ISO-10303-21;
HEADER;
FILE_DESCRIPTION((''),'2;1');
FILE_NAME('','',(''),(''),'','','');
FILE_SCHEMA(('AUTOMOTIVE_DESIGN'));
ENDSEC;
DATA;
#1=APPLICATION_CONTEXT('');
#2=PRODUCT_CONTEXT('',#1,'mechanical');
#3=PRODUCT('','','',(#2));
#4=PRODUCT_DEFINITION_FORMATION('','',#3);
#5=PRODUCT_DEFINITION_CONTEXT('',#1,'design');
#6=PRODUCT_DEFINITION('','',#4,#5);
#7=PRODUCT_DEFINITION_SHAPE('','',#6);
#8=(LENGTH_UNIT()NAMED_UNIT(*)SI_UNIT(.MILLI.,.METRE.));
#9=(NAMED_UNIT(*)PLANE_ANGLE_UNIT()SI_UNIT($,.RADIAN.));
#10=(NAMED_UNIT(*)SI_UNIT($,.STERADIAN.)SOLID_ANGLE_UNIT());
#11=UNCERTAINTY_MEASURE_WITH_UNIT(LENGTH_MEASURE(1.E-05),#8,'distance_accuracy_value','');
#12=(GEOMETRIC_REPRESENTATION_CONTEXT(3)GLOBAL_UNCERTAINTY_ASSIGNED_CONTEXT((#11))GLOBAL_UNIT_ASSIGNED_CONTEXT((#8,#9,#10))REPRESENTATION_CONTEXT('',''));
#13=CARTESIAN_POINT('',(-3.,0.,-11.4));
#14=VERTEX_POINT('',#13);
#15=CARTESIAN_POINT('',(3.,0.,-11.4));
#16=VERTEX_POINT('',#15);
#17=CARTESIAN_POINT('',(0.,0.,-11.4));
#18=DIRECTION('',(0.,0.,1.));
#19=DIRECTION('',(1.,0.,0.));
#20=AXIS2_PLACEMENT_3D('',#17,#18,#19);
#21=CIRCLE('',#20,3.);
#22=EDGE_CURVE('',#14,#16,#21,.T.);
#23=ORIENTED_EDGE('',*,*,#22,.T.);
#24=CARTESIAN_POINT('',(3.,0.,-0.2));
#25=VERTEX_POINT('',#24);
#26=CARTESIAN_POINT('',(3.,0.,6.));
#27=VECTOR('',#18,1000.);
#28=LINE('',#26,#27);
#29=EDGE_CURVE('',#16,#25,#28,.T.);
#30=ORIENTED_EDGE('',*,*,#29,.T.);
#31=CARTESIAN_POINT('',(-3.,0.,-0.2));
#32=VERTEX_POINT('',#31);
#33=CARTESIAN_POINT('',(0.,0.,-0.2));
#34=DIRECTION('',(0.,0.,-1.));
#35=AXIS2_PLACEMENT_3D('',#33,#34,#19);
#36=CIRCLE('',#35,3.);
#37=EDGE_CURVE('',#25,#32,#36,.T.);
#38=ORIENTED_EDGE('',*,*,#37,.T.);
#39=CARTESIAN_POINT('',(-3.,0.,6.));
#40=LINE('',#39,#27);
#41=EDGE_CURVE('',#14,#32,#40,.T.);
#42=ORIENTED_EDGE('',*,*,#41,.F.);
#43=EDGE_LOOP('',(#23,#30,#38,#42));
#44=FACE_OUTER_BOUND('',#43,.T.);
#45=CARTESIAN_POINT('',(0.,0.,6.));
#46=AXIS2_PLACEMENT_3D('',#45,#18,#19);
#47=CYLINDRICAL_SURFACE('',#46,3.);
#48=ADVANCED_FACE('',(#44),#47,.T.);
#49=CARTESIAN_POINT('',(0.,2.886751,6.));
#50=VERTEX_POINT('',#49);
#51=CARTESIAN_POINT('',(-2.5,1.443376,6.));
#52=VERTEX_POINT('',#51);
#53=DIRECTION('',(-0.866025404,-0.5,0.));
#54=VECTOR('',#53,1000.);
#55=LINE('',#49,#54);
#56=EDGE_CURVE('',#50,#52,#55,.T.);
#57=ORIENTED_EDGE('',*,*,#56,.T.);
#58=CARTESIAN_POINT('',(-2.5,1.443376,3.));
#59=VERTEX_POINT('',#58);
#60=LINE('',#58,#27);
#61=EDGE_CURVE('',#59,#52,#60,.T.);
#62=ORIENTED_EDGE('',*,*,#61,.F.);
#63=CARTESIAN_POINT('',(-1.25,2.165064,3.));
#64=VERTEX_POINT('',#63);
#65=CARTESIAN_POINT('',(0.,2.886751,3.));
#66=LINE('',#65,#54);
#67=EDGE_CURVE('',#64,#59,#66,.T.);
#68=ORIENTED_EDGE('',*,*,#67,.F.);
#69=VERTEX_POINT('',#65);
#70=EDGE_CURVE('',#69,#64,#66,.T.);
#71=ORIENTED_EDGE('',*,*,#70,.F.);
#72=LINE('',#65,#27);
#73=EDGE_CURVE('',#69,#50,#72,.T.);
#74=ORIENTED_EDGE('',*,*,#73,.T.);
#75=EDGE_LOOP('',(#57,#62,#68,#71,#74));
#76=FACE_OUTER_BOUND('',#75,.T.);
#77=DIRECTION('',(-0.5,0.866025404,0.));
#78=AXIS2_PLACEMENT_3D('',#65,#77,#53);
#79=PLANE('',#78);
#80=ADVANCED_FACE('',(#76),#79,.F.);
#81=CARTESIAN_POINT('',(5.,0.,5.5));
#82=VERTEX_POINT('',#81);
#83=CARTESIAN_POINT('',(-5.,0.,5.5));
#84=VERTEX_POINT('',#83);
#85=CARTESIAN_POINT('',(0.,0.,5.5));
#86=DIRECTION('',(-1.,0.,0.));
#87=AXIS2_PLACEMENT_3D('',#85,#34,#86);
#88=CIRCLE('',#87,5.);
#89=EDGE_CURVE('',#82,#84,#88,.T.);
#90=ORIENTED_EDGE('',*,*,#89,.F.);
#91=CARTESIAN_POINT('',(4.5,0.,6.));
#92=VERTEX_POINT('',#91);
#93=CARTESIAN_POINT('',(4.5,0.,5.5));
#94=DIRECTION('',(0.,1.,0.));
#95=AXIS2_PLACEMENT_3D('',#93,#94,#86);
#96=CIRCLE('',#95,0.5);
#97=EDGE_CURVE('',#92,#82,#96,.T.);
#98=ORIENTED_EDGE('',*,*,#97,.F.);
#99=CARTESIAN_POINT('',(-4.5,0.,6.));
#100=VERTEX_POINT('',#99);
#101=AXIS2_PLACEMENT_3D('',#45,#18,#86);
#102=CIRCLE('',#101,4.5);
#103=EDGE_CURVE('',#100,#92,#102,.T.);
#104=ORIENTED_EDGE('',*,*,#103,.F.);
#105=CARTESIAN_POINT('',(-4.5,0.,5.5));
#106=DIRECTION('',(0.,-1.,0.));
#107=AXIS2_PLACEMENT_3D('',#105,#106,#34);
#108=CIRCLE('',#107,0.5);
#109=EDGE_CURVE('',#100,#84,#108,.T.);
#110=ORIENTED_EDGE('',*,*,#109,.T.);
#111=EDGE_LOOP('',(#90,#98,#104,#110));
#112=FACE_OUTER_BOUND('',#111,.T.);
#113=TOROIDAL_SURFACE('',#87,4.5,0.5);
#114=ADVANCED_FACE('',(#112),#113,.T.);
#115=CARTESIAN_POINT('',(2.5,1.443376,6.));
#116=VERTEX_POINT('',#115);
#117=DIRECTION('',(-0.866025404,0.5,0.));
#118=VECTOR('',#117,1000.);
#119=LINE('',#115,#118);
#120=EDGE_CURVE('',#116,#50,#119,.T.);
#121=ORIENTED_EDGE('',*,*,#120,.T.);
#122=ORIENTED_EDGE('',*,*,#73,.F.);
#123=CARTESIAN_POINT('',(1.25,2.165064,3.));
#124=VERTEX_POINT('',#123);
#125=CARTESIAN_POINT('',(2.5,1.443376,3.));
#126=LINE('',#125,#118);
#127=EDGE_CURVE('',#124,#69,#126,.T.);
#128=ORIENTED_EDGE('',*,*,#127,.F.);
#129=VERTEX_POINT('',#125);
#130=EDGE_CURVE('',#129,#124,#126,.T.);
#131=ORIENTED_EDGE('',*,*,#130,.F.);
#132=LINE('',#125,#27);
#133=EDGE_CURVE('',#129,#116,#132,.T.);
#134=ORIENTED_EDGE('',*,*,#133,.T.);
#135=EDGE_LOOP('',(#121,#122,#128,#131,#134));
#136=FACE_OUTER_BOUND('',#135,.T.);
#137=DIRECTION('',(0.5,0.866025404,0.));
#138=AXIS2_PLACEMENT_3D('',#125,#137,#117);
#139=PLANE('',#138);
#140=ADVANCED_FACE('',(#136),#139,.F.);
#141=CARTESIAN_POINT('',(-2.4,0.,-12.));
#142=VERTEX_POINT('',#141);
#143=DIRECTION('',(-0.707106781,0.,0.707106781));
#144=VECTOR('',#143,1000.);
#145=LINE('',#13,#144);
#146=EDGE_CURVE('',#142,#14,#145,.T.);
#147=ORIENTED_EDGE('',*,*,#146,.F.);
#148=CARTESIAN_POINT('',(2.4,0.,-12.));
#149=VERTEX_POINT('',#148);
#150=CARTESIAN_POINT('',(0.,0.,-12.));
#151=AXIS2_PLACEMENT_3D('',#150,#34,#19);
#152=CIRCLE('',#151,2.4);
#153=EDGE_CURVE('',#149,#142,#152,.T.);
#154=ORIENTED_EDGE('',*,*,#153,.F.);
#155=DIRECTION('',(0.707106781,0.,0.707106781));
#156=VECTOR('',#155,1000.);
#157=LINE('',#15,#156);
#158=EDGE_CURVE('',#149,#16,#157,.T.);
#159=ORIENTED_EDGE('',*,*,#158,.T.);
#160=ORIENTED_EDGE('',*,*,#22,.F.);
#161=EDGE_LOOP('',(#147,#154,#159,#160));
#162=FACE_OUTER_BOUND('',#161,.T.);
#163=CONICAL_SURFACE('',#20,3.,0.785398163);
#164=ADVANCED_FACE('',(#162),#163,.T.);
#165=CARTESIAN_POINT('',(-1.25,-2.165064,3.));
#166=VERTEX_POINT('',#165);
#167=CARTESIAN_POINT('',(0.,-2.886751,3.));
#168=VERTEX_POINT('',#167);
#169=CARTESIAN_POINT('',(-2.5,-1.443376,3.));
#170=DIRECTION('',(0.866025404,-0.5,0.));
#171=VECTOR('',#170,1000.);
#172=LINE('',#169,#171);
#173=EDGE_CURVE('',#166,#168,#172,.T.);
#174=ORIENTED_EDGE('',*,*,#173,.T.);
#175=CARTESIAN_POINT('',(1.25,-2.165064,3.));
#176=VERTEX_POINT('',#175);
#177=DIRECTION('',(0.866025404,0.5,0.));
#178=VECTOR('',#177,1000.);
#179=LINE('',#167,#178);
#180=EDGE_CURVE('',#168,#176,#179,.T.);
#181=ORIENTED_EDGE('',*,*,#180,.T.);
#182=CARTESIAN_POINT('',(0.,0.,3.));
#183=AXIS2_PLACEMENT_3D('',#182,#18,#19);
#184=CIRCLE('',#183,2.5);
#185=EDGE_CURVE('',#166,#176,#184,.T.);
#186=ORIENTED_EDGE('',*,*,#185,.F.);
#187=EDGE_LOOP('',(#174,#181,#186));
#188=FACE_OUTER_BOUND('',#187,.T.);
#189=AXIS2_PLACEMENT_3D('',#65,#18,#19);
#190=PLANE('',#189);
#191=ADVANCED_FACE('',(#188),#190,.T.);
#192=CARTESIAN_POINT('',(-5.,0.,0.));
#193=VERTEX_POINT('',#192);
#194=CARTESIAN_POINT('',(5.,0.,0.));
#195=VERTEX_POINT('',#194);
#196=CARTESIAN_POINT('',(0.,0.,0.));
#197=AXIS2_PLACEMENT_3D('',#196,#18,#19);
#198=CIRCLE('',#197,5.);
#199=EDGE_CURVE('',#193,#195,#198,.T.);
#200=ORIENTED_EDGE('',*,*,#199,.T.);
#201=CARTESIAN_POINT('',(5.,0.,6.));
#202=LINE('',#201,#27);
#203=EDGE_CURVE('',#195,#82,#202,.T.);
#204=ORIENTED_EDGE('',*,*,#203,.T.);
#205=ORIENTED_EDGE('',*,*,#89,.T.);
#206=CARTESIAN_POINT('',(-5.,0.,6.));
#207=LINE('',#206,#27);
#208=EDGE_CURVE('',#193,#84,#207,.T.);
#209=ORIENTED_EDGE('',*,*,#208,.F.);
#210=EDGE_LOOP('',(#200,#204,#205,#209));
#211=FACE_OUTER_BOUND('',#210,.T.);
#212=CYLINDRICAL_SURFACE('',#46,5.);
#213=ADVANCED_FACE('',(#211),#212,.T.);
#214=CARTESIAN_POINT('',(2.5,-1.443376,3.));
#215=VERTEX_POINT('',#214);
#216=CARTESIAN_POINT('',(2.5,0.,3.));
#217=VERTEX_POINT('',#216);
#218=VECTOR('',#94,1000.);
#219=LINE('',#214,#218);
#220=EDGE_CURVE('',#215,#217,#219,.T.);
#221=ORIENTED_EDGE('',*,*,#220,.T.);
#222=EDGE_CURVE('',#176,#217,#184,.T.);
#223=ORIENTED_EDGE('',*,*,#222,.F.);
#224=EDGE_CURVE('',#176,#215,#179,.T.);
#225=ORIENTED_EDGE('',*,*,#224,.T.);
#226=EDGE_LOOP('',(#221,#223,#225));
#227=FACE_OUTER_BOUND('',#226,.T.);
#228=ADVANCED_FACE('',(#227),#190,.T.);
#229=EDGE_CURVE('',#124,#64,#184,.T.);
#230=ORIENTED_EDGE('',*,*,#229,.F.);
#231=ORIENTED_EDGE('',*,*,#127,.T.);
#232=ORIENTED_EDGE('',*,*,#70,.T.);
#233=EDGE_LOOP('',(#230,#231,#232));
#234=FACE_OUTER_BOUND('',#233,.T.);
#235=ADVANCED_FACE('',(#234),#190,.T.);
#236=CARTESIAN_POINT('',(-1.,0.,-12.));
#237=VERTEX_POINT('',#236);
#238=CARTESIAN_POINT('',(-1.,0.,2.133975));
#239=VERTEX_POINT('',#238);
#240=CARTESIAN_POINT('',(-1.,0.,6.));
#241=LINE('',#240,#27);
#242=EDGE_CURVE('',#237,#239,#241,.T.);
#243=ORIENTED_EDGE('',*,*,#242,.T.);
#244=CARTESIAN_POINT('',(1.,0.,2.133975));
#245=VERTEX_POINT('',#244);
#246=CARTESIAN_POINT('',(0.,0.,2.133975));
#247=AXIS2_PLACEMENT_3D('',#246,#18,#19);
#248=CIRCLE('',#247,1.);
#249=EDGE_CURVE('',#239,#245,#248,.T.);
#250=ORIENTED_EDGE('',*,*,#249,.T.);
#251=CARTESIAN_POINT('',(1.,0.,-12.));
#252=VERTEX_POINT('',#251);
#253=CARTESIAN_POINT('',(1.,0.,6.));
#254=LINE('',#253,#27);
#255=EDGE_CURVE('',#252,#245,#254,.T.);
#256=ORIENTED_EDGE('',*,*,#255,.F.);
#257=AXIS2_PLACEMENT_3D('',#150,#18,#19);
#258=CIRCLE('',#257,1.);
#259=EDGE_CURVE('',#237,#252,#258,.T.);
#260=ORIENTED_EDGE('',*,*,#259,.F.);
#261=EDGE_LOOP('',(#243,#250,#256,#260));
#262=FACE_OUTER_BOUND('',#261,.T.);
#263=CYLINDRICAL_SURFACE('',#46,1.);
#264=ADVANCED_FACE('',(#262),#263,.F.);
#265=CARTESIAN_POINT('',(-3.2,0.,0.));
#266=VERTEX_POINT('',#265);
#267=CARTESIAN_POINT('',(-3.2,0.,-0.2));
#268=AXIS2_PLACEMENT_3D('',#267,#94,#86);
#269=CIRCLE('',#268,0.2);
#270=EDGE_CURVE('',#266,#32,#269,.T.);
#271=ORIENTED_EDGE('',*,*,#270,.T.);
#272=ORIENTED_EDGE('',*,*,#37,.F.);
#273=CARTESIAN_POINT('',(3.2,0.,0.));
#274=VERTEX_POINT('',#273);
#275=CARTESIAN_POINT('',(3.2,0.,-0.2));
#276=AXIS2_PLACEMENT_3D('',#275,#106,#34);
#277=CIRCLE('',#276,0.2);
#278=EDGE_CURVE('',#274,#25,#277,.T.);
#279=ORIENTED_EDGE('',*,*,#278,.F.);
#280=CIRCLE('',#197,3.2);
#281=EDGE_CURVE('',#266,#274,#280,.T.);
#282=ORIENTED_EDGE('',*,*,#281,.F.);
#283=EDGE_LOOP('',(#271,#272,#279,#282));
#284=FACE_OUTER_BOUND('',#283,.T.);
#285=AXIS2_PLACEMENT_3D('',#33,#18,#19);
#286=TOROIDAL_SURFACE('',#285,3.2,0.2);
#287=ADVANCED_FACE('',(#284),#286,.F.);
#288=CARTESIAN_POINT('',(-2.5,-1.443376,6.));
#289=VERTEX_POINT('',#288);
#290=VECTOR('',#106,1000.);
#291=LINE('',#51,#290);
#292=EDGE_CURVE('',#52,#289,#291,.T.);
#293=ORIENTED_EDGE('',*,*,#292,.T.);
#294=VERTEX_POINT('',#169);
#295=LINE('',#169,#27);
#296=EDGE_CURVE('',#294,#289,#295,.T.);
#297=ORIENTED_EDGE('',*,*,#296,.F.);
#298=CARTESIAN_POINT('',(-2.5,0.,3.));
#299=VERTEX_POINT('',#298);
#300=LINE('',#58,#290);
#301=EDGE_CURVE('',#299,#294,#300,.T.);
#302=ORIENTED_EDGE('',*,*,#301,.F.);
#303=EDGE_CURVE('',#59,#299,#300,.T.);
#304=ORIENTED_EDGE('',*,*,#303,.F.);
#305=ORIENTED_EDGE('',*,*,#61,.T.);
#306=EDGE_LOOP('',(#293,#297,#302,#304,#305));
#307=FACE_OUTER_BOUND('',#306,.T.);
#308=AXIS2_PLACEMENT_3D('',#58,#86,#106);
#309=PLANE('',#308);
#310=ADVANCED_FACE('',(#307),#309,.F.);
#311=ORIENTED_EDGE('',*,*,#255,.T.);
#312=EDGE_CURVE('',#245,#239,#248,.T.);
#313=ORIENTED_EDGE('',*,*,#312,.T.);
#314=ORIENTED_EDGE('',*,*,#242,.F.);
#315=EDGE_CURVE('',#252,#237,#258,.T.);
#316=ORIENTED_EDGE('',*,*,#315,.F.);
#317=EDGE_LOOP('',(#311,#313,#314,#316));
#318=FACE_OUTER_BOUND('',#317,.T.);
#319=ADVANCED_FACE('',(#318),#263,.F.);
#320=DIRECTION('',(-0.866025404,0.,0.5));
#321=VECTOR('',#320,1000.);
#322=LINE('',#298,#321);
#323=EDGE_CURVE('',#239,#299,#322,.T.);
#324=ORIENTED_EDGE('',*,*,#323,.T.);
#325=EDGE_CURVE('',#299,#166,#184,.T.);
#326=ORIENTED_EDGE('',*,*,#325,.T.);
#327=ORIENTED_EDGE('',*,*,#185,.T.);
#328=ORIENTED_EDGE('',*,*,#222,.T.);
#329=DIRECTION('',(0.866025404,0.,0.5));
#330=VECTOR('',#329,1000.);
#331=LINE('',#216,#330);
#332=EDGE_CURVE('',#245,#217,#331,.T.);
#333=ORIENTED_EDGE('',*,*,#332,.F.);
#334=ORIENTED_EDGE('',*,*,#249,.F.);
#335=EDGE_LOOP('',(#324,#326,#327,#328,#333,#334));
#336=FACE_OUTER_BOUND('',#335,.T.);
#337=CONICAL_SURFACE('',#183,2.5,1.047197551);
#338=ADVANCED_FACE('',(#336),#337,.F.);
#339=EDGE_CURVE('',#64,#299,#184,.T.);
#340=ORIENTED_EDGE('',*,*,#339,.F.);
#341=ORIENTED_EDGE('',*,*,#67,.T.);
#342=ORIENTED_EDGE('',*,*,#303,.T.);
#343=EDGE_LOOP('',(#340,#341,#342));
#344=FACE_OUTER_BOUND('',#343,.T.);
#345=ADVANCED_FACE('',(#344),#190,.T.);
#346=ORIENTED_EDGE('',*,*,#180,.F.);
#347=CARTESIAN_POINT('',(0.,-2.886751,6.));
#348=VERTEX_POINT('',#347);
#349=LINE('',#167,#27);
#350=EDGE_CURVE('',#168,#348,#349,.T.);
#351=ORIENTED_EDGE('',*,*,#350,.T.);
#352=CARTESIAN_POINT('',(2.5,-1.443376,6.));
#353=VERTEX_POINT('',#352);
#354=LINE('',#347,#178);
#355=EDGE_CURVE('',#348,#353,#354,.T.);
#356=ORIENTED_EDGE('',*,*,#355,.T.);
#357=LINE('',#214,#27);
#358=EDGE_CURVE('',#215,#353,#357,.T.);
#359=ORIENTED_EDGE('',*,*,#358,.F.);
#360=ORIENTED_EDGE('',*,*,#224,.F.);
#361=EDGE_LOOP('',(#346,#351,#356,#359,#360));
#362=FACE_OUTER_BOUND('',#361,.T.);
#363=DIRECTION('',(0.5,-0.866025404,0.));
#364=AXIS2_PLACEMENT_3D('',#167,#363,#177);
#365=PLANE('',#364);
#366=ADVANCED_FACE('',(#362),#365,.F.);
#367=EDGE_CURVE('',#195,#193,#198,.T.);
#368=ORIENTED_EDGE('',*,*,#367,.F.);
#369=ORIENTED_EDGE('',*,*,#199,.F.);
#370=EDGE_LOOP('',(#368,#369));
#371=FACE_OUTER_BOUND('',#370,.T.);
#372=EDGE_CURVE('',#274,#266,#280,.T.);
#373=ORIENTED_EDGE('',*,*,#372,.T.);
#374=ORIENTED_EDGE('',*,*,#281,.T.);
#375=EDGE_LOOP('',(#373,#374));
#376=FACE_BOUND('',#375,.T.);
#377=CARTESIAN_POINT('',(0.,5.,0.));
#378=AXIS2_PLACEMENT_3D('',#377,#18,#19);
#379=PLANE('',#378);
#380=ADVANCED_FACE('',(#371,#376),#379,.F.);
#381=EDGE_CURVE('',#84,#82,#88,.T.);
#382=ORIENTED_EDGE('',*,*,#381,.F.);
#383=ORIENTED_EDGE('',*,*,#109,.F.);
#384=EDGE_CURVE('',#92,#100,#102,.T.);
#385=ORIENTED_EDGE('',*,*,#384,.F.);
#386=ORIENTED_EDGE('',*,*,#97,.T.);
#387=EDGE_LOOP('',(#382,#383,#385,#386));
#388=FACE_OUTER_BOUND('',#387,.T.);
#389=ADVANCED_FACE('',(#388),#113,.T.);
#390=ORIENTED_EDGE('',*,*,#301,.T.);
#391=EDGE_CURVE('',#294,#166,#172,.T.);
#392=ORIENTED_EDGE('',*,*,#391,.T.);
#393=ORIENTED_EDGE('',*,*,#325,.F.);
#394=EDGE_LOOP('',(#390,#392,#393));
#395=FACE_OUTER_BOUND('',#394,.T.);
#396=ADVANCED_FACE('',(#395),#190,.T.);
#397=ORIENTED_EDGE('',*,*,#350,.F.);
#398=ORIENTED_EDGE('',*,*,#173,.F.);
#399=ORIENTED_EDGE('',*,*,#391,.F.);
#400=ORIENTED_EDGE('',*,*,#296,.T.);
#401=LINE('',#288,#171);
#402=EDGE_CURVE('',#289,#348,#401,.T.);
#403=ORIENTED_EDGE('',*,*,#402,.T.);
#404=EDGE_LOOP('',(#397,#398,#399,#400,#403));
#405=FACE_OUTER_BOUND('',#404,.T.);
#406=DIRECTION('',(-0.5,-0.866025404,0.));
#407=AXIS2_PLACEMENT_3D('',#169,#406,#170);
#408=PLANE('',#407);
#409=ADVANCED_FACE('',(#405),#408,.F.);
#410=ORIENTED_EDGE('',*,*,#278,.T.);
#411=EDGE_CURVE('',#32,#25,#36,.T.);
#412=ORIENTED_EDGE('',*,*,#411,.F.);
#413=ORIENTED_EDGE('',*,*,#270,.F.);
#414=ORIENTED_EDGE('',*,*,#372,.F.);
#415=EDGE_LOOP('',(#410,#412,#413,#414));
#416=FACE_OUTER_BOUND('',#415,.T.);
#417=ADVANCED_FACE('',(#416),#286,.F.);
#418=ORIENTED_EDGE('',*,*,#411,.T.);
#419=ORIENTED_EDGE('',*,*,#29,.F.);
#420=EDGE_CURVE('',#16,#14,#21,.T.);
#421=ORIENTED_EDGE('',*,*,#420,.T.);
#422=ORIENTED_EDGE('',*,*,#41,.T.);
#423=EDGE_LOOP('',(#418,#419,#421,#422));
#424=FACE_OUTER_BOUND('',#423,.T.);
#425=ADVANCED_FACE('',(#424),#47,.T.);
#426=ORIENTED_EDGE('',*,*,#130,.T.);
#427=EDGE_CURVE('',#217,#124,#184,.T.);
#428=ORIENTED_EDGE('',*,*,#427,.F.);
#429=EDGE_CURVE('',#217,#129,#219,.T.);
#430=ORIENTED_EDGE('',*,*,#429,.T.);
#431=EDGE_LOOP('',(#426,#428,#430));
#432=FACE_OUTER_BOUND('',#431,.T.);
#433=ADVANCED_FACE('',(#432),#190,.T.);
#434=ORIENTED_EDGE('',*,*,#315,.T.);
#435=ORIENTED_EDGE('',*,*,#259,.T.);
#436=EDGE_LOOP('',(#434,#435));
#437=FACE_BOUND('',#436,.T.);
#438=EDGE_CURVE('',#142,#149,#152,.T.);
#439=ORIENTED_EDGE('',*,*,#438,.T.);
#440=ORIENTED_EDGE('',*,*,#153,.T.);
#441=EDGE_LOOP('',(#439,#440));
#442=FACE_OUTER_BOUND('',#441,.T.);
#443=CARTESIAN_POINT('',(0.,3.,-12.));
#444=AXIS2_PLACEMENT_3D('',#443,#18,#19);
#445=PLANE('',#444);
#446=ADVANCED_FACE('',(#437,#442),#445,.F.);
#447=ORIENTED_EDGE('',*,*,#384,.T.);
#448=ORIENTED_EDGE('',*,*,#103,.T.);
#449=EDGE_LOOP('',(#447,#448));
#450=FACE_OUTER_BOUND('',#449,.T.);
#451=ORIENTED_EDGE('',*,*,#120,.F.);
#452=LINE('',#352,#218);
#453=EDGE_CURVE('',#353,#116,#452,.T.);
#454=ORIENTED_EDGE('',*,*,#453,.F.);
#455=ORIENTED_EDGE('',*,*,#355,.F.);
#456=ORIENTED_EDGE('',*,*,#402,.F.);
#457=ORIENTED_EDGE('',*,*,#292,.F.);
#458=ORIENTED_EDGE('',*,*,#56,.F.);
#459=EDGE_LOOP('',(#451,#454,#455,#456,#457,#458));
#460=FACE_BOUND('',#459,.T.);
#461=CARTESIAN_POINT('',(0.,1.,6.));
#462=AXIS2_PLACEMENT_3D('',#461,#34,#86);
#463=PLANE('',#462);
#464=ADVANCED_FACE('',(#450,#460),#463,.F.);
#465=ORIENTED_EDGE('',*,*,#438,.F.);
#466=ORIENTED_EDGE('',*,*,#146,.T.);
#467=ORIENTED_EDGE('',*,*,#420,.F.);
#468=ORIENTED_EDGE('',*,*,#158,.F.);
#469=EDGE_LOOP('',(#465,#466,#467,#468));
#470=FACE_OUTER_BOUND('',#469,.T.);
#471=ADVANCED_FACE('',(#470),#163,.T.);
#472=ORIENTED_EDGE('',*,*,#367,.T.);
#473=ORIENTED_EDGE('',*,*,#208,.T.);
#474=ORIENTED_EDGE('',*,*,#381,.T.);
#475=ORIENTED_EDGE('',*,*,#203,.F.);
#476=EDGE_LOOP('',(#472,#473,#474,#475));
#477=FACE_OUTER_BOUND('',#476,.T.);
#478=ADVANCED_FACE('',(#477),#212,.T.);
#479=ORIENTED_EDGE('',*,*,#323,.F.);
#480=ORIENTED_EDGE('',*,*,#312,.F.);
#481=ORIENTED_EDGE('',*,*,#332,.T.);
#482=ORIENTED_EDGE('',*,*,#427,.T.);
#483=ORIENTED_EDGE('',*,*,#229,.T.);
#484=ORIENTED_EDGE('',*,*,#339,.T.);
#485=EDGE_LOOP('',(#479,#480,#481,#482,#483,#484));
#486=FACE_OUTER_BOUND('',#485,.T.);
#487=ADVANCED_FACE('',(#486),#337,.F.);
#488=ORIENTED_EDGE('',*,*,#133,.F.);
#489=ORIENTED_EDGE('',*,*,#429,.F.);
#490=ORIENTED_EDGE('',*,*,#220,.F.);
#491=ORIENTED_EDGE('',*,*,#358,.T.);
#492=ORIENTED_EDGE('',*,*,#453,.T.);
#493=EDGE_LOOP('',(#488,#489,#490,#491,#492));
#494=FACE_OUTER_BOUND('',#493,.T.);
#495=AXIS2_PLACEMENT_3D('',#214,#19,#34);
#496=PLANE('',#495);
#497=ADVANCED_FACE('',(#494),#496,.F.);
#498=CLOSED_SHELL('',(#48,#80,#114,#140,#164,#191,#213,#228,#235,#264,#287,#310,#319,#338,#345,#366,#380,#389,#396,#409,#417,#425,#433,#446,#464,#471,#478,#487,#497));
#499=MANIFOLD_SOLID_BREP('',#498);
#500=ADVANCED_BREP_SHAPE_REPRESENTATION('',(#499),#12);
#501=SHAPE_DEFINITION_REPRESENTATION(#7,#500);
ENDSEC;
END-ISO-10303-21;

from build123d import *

# Parameters (mm, degrees)
CUT_EXTRUDE1_DEPTH = 3
FILLET1_R          = 0.5
CHAMFER1_SIZE      = 0.6
FILLET2_R          = 0.2


with BuildPart() as part:
    # Sketch3 → Revolve1 (revolve)
    with BuildSketch(Plane(origin=(0, 0, 0), x_dir=(0, 0, -1), z_dir=(1, 0, 0)), mode=Mode.PRIVATE) as revolve1_sk:
        Polygon((-6, 1), (-6, 5), (0, 5), (0, 3), (12, 3), (12, 1), align=None)
    revolve(revolve1_sk.sketch.rotate(Axis((0, 0, 6), (0, 0, -1)), 90), axis=Axis((0, 0, 6), (0, 0, -1)))

    # Sketch4 → Cut-Extrude1 (cut)
    with BuildSketch(Plane.XY.offset(6)):
        Polygon((0, 2.886751346), (-2.5, 1.443375673), (-2.5, -1.443375673), (0, -2.886751346), (2.5, -1.443375673), (2.5, 1.443375673), align=None)
    extrude(amount=-CUT_EXTRUDE1_DEPTH, mode=Mode.SUBTRACT)

    # Fillet1
    fillet1_edges = [part.edges().sort_by_distance(p)[0] for p in [
        (-5, 0, 6),
    ]]
    fillet(fillet1_edges, radius=FILLET1_R)

    # Chamfer1
    chamfer1_edges = [part.edges().sort_by_distance(p)[0] for p in [
        (-3, 0, -12),
    ]]
    chamfer(chamfer1_edges, length=CHAMFER1_SIZE)

    # Cut-Extrude2 cone 1 section (through the dimple's axis) → Cut-Extrude2 (revolve, cut)
    with BuildSketch(Plane(origin=(0, 0, 3), x_dir=(0, -1, 0), z_dir=(1, 0, 0))):
        Polygon((0, 0), (2.5, 0), (0, 1.443375673), align=None)
    revolve(axis=Axis((0, 0, 3), (0, 0, -1)), mode=Mode.SUBTRACT)

    # Fillet2
    fillet2_edges = [part.edges().sort_by_distance(p)[0] for p in [
        (-3, 0, 0),
    ]]
    fillet(fillet2_edges, radius=FILLET2_R)


solid = part.part
